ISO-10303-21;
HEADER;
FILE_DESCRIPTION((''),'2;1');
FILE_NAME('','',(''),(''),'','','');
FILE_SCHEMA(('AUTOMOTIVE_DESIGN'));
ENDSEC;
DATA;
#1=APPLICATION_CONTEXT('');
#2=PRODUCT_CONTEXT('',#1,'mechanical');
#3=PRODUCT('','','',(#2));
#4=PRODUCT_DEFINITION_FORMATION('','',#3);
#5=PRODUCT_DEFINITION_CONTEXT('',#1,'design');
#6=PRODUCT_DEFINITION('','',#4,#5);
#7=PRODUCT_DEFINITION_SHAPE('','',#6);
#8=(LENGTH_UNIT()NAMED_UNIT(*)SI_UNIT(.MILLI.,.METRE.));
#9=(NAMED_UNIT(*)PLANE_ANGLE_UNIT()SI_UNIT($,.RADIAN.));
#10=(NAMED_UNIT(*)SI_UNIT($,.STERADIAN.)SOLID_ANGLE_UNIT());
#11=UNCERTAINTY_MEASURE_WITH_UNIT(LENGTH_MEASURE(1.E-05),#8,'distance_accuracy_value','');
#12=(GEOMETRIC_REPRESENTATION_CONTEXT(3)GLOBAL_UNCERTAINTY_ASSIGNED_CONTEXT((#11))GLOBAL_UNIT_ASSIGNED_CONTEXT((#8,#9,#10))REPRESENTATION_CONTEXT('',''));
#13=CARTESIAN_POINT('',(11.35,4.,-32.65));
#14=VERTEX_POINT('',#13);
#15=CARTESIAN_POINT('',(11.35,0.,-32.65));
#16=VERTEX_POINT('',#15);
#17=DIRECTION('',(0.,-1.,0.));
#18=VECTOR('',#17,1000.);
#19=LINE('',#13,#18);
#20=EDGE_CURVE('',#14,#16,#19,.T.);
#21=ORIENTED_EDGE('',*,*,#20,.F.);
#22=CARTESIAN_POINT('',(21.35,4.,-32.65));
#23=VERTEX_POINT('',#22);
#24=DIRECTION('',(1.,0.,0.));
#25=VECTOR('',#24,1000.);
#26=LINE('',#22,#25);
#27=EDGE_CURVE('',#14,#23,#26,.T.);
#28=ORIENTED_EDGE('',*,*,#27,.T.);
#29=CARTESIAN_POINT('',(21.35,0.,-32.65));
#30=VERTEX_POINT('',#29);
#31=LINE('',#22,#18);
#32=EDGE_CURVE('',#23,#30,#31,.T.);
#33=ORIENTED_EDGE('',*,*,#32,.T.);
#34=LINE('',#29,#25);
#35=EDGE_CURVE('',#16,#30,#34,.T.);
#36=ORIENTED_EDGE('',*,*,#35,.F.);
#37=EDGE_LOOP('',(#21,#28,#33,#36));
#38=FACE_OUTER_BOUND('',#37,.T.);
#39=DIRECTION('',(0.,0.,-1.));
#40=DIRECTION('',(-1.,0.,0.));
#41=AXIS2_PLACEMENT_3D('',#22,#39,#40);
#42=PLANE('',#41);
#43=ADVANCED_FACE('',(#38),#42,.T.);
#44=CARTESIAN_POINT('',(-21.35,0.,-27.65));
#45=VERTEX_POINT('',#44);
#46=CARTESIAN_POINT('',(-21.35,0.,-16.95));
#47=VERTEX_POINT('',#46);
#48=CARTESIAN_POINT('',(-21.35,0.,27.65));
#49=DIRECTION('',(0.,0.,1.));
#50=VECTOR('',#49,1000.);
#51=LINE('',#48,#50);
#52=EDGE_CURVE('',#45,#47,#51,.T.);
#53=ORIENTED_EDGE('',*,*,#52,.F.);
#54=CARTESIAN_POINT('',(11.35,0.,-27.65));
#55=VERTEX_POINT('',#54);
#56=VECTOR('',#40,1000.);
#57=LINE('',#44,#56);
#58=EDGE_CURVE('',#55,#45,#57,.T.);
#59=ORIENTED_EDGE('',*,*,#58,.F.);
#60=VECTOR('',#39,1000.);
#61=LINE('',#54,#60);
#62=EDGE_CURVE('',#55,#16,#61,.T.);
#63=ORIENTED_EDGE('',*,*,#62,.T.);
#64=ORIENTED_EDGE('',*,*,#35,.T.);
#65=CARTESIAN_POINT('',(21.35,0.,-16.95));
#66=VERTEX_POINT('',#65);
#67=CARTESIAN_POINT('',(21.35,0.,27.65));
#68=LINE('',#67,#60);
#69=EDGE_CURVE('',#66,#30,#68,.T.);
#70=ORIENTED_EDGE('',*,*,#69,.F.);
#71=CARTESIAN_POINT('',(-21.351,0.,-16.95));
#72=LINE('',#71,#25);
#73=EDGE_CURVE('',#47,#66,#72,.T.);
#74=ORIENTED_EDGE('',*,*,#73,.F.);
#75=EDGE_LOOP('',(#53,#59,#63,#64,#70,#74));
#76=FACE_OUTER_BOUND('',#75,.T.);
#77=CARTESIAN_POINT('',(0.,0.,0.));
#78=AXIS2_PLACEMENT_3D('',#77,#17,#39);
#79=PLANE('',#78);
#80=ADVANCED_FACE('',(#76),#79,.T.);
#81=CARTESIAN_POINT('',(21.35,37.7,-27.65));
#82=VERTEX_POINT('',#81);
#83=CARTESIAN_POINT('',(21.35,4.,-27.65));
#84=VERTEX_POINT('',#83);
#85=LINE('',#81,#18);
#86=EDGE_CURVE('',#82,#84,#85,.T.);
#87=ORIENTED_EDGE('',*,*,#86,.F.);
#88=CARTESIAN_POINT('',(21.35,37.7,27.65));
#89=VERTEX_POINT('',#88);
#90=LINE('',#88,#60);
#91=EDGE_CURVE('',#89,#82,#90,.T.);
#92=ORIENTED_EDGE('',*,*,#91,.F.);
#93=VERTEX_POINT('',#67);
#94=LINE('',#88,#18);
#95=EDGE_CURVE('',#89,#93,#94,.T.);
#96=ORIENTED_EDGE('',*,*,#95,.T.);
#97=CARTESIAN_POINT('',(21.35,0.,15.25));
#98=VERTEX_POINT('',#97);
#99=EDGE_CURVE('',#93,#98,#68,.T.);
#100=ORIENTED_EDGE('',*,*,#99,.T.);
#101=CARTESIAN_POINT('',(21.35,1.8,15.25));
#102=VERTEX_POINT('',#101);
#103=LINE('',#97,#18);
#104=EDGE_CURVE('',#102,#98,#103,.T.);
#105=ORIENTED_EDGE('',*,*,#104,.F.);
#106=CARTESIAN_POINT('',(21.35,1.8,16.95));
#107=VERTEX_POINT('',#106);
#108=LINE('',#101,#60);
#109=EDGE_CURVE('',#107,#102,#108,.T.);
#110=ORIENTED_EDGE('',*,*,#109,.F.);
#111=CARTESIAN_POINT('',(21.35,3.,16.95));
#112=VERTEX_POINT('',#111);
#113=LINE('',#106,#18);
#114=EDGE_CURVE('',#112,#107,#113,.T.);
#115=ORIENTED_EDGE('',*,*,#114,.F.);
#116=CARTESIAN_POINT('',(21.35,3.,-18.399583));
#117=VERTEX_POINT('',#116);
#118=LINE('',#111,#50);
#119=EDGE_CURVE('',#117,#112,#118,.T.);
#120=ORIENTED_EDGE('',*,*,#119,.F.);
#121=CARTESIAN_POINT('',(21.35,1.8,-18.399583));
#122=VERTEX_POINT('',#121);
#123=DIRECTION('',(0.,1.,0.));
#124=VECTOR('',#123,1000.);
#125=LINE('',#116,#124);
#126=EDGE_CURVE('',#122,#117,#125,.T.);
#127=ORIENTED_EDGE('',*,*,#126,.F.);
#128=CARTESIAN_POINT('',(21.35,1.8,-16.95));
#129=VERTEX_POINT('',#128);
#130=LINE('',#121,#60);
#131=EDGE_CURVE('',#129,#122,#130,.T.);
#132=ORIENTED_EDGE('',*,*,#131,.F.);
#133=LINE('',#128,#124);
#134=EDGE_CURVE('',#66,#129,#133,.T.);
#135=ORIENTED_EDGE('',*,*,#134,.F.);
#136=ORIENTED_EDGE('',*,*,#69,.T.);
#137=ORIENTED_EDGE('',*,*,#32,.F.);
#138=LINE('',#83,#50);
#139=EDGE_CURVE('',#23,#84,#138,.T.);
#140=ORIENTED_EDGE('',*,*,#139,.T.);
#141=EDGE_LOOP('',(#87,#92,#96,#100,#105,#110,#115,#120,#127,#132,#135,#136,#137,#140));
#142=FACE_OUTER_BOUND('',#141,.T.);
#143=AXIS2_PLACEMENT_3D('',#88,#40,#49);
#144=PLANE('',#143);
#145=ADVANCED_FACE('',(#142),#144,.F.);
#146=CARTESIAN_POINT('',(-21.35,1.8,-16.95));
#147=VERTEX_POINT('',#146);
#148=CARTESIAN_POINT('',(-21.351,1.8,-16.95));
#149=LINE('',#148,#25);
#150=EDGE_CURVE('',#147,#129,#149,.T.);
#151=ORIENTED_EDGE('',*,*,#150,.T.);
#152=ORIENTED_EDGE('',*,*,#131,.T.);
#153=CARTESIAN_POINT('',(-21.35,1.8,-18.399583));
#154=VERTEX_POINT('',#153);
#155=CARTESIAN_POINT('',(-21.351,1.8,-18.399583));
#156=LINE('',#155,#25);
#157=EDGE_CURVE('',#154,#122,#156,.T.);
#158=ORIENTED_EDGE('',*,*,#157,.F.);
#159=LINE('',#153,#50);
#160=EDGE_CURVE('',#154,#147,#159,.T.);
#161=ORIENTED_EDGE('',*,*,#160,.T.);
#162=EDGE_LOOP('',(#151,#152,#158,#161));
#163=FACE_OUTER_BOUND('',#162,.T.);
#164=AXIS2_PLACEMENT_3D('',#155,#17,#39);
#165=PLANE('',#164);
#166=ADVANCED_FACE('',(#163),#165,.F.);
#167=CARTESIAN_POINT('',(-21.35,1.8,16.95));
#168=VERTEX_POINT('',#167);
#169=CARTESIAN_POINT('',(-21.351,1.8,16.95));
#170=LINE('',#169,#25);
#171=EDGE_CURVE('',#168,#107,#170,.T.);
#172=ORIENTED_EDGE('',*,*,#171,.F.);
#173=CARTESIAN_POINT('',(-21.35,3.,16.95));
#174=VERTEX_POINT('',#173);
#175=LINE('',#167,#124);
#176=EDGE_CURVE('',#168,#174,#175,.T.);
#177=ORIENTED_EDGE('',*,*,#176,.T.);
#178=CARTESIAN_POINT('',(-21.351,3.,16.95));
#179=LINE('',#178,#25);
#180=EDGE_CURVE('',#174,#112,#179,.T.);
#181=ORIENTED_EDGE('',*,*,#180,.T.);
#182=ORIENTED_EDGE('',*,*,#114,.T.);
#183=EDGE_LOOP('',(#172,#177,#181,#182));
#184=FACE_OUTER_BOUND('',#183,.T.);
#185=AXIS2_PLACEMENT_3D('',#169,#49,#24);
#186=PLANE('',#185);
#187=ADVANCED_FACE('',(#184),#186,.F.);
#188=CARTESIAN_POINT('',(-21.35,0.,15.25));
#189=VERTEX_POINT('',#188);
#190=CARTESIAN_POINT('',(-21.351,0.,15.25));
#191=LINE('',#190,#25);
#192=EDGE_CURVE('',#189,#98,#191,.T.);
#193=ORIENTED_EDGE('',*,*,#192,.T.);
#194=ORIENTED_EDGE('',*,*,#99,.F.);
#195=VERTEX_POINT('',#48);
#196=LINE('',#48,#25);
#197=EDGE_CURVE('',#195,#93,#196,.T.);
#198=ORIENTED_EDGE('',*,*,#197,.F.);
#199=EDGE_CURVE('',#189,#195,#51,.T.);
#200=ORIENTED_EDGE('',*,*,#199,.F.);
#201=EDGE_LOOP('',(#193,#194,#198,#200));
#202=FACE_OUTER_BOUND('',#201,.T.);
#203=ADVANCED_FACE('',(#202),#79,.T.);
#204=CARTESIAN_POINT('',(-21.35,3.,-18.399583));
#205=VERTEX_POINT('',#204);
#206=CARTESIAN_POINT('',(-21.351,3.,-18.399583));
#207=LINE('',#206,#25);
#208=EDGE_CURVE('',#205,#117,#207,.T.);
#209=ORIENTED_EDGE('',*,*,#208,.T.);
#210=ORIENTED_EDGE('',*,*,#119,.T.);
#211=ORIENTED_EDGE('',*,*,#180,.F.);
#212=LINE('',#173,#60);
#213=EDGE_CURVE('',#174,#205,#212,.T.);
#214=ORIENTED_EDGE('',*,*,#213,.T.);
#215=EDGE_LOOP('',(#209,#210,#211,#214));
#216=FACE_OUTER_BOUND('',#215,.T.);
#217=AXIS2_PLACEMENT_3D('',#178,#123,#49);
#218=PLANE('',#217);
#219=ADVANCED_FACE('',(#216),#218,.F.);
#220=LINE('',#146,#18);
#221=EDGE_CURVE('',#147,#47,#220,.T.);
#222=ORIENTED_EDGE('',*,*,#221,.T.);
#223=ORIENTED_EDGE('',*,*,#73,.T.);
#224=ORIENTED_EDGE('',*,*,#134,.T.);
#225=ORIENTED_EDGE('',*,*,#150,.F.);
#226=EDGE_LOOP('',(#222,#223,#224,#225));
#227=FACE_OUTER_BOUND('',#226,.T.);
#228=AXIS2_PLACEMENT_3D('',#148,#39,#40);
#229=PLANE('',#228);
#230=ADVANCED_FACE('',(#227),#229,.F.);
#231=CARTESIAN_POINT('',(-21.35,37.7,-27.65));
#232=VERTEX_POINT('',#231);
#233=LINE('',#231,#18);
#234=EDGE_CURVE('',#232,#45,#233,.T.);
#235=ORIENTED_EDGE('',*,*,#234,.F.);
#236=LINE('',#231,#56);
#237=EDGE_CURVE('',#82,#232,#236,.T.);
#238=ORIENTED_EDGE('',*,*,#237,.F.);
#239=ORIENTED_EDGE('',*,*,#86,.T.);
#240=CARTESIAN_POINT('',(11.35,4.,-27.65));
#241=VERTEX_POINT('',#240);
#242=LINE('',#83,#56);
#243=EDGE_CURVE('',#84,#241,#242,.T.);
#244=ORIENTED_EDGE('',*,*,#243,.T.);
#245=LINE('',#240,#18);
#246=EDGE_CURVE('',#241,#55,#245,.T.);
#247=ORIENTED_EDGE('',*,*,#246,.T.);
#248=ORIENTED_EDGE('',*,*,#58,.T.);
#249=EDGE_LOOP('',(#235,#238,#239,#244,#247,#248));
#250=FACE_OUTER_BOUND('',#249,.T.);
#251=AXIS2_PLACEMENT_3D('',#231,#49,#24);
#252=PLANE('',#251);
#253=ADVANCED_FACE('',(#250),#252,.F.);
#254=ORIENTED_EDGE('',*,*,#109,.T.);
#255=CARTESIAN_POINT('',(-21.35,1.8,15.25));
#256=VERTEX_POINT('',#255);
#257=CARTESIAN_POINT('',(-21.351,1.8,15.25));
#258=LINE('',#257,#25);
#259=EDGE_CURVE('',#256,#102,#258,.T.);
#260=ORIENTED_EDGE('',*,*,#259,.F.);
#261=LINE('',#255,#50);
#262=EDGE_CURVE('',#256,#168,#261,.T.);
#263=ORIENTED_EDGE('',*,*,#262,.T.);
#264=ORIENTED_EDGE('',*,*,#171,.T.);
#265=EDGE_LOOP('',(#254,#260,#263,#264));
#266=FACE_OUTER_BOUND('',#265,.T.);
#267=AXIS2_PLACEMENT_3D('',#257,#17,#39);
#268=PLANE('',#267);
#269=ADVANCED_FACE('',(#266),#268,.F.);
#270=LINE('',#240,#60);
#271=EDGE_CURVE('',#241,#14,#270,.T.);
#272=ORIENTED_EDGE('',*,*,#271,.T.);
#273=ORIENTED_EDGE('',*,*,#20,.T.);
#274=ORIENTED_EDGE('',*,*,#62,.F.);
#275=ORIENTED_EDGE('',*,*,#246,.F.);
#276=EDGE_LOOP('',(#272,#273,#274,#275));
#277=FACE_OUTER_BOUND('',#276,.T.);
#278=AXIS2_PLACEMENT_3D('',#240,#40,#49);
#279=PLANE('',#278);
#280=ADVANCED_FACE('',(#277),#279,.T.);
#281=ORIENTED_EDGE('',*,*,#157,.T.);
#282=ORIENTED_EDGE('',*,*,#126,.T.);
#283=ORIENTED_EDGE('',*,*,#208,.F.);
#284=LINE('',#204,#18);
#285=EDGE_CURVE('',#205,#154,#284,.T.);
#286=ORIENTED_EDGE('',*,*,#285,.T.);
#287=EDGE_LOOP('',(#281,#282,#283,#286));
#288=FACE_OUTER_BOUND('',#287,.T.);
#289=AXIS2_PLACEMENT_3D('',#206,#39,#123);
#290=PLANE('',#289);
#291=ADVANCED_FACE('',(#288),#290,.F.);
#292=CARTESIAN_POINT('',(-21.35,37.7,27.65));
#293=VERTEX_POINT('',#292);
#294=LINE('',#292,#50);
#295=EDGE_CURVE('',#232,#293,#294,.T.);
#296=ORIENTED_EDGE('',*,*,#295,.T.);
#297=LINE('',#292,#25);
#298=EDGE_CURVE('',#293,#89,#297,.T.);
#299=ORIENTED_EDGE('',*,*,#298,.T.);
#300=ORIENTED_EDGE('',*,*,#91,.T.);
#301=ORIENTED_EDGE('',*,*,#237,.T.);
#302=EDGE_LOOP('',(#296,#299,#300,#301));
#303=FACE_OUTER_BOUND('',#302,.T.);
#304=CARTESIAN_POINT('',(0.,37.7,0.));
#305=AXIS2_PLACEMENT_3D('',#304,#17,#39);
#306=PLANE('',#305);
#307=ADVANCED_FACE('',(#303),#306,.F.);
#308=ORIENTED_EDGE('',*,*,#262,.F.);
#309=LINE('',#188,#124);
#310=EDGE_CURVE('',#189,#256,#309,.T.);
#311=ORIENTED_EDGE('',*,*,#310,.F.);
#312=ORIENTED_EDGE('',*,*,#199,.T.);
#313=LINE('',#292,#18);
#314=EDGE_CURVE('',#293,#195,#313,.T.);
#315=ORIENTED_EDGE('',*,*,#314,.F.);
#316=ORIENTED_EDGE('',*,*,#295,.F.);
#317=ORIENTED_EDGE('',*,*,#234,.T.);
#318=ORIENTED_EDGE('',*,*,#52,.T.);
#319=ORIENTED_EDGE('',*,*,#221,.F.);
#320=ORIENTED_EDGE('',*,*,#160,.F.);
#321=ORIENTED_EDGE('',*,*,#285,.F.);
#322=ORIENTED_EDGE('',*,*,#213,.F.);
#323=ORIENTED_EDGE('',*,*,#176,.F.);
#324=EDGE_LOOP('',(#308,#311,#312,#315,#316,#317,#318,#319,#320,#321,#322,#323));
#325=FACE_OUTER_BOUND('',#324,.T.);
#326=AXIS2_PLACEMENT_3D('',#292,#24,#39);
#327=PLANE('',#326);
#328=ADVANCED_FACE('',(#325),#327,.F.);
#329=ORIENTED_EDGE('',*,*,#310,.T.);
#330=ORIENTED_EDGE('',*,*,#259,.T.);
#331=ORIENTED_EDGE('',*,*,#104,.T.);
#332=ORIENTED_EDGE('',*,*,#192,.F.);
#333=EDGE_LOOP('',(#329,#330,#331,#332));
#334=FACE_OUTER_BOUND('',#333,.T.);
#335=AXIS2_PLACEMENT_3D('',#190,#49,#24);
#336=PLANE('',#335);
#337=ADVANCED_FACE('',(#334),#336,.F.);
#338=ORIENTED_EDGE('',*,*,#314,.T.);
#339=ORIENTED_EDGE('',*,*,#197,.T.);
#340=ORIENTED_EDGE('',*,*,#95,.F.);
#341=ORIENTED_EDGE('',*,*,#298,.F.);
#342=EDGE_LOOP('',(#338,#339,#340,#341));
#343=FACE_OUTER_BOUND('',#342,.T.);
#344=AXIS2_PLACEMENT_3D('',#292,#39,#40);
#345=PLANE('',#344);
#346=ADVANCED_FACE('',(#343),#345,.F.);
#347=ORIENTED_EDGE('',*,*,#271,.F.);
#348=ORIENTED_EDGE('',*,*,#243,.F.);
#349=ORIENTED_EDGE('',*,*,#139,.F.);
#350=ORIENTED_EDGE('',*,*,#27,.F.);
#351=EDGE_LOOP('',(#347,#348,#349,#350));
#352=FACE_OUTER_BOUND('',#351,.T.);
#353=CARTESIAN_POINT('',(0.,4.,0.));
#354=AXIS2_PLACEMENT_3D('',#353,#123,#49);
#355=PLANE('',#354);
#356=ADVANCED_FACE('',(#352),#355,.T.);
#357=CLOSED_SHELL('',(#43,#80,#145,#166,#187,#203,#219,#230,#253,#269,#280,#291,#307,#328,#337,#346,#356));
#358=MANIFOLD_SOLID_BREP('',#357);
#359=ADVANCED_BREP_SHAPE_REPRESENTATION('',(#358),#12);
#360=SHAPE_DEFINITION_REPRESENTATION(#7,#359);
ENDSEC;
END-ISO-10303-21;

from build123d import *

# Parameters (mm, degrees)
SKETCH1_W           = 42.7
SKETCH1_H           = 55.3
BOSS_EXTRUDE1_DEPTH = 37.7
CUT_EXTRUDE1_REACH  = 65.317
SKETCH4_W           = 10
SKETCH4_H           = 5
BOSS_EXTRUDE2_DEPTH = 4


with BuildPart() as part:
    # Sketch1 → Boss-Extrude1 (new body)
    with BuildSketch(Plane(origin=(0, 0, 0), x_dir=(1, 0, 0), z_dir=(0, 1, 0))):
        Rectangle(SKETCH1_W, SKETCH1_H)
    extrude(amount=BOSS_EXTRUDE1_DEPTH)

    # Sketch3 → Cut-Extrude1 (cut, up to next)
    with BuildSketch(Plane(origin=(21.35, 0, 0), x_dir=(0, 0, -1), z_dir=(1, 0, 0)), mode=Mode.PRIVATE) as cut_extrude1_sk1:
        Polygon((-15.25, 0), (-15.25, 1.8), (-16.95, 1.8), (-16.95, 3), (18.399583247, 3), (18.399583247, 1.8), (16.95, 1.8), (16.95, 0), align=None)
    cut_extrude1_tool1 = extrude(cut_extrude1_sk1.sketch, amount=-CUT_EXTRUDE1_REACH, mode=Mode.PRIVATE) & part.part
    add(cut_extrude1_tool1.solids().sort_by_distance((21.35, 1.533887, -0.797088))[0], mode=Mode.SUBTRACT)

    # Sketch4 → Boss-Extrude2 (add)
    with BuildSketch(Plane.XZ):
        with Locations((16.35, -30.15)):
            Rectangle(SKETCH4_W, SKETCH4_H)
    extrude(amount=-BOSS_EXTRUDE2_DEPTH)


solid = part.part
